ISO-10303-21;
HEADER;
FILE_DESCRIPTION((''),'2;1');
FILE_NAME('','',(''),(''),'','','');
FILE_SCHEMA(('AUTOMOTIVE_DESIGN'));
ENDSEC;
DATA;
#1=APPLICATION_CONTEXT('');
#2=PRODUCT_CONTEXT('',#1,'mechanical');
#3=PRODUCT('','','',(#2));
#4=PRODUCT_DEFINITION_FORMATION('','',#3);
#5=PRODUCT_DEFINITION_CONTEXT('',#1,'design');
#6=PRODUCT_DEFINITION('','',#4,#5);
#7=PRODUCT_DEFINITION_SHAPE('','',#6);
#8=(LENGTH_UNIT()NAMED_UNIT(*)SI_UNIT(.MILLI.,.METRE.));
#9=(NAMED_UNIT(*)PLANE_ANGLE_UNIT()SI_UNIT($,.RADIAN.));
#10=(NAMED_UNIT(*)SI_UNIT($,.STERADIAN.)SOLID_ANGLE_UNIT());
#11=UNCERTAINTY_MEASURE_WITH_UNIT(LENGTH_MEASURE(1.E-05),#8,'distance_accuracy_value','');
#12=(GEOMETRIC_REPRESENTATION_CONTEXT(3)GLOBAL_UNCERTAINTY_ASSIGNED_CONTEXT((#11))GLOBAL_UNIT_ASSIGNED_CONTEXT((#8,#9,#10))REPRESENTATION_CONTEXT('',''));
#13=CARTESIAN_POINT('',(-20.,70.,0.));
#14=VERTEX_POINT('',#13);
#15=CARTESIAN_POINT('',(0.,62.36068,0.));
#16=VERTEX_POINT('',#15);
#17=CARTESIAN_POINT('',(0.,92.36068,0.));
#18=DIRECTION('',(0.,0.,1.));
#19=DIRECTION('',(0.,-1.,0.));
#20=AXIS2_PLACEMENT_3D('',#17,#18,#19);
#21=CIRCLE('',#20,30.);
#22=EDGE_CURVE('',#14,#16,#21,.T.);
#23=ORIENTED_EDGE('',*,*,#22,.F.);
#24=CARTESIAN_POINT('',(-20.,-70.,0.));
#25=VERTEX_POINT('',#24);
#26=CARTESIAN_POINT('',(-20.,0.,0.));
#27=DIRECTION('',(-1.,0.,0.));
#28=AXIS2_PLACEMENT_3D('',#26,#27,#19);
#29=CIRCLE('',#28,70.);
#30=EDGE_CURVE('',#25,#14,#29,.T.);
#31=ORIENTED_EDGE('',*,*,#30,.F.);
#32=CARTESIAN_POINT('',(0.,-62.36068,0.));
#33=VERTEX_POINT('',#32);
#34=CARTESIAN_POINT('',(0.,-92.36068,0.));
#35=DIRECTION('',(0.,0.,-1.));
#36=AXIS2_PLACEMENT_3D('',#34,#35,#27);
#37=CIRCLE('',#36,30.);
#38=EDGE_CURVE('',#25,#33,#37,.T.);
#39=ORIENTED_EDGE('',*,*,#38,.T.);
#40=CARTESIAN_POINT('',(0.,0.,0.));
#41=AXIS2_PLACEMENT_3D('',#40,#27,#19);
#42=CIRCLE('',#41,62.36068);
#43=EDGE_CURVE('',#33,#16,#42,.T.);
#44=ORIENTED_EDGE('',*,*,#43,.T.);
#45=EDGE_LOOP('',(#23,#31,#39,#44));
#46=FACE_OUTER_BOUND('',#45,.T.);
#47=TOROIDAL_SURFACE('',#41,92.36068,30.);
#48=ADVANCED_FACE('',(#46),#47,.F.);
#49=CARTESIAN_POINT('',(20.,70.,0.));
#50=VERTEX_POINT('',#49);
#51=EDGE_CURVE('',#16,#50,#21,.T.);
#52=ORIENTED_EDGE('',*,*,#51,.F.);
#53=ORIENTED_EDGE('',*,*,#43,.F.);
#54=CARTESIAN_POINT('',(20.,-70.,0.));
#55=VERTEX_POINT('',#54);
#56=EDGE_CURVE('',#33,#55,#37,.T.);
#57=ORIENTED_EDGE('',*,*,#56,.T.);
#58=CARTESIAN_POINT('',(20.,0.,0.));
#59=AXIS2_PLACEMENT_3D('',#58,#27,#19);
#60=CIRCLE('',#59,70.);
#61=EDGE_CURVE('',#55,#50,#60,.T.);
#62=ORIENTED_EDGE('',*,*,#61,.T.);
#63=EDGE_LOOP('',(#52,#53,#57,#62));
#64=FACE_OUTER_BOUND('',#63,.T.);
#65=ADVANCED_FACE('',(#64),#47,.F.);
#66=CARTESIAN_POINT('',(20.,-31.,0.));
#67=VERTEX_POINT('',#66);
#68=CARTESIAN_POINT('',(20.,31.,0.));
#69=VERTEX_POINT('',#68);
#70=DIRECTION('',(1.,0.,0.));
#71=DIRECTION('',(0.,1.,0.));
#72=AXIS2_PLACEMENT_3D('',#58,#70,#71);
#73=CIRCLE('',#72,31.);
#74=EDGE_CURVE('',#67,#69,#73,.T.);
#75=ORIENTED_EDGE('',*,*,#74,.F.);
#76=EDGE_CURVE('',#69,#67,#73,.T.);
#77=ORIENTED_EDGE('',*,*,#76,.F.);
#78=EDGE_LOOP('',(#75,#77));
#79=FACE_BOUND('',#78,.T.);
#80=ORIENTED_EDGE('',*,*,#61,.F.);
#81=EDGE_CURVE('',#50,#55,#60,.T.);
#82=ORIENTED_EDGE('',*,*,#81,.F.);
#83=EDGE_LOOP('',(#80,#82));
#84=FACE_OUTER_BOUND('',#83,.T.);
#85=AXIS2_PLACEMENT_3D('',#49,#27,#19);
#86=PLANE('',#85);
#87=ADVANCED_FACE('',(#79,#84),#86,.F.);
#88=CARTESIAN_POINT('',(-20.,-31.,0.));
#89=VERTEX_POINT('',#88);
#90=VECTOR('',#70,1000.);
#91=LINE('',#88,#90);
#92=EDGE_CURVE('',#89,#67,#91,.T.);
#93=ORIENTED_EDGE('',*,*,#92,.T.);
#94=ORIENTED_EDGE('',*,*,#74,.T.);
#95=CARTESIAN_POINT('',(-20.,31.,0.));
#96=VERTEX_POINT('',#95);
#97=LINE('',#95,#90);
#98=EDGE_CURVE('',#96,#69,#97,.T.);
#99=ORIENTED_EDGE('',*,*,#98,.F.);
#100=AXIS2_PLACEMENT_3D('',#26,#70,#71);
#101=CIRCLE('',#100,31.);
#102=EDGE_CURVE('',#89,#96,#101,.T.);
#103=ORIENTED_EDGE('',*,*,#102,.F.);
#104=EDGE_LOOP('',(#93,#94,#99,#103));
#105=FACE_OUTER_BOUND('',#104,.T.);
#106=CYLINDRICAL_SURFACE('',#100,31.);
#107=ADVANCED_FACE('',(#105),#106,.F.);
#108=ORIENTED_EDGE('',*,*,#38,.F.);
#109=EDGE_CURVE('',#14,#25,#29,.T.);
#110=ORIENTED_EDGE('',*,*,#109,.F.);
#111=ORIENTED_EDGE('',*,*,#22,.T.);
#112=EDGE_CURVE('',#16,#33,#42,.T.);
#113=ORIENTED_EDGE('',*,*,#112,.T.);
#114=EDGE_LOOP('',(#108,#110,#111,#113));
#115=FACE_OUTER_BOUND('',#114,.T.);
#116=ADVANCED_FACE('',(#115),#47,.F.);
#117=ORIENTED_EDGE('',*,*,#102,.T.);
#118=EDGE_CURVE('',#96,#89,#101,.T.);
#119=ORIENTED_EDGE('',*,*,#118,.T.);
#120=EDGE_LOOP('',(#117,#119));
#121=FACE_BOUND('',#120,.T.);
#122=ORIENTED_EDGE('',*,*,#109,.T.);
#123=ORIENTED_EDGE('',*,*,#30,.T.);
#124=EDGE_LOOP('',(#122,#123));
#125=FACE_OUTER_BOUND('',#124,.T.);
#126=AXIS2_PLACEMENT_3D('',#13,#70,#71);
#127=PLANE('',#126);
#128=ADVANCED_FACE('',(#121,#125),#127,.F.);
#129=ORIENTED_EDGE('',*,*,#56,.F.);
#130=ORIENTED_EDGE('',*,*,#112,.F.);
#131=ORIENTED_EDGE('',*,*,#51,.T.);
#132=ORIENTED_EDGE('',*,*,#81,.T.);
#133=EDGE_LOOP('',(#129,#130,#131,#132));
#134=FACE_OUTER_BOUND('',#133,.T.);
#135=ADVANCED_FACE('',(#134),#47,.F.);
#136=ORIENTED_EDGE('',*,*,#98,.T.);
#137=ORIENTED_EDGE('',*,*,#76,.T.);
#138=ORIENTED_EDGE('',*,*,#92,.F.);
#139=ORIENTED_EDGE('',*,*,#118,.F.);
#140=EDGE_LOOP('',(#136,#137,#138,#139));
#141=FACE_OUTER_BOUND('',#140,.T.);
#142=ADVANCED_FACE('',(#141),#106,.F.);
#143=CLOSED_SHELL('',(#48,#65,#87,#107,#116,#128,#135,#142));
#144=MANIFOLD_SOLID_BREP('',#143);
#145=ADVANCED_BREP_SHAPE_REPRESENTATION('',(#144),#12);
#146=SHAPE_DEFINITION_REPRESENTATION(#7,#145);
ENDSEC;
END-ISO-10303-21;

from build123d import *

# Parameters (mm, degrees)
SKETCH_2_R          = 31
CUT_EXTRUDE_1_DEPTH = 107.77078252


with BuildPart() as part:
    # 草图1 → 旋转1 (revolve)
    with BuildSketch(Plane.XY, mode=Mode.PRIVATE) as revolve_1_sk:
        with BuildLine():
            Line((-20, 70), (-20, 0))
            Line((-20, 0), (20, 0))
            Line((20, 0), (20, 70))
            ThreePointArc((20, 70), (0, 62.360679775), (-20, 70))
        make_face()
    revolve(revolve_1_sk.sketch.rotate(Axis((-20, 0, 0), (1, 0, 0)), 180), axis=Axis((-20, 0, 0), (1, 0, 0)))

    # 草图2 → 切除-拉伸1 (cut, through all)
    with BuildSketch(Plane(origin=(20, 0, 0), x_dir=(0, 0, -1), z_dir=(1, 0, 0))):
        with Locations(Location((0, 0, 0), (0, 0, 90))):
            Circle(SKETCH_2_R)
    extrude(amount=-CUT_EXTRUDE_1_DEPTH, mode=Mode.SUBTRACT)


solid = part.part
